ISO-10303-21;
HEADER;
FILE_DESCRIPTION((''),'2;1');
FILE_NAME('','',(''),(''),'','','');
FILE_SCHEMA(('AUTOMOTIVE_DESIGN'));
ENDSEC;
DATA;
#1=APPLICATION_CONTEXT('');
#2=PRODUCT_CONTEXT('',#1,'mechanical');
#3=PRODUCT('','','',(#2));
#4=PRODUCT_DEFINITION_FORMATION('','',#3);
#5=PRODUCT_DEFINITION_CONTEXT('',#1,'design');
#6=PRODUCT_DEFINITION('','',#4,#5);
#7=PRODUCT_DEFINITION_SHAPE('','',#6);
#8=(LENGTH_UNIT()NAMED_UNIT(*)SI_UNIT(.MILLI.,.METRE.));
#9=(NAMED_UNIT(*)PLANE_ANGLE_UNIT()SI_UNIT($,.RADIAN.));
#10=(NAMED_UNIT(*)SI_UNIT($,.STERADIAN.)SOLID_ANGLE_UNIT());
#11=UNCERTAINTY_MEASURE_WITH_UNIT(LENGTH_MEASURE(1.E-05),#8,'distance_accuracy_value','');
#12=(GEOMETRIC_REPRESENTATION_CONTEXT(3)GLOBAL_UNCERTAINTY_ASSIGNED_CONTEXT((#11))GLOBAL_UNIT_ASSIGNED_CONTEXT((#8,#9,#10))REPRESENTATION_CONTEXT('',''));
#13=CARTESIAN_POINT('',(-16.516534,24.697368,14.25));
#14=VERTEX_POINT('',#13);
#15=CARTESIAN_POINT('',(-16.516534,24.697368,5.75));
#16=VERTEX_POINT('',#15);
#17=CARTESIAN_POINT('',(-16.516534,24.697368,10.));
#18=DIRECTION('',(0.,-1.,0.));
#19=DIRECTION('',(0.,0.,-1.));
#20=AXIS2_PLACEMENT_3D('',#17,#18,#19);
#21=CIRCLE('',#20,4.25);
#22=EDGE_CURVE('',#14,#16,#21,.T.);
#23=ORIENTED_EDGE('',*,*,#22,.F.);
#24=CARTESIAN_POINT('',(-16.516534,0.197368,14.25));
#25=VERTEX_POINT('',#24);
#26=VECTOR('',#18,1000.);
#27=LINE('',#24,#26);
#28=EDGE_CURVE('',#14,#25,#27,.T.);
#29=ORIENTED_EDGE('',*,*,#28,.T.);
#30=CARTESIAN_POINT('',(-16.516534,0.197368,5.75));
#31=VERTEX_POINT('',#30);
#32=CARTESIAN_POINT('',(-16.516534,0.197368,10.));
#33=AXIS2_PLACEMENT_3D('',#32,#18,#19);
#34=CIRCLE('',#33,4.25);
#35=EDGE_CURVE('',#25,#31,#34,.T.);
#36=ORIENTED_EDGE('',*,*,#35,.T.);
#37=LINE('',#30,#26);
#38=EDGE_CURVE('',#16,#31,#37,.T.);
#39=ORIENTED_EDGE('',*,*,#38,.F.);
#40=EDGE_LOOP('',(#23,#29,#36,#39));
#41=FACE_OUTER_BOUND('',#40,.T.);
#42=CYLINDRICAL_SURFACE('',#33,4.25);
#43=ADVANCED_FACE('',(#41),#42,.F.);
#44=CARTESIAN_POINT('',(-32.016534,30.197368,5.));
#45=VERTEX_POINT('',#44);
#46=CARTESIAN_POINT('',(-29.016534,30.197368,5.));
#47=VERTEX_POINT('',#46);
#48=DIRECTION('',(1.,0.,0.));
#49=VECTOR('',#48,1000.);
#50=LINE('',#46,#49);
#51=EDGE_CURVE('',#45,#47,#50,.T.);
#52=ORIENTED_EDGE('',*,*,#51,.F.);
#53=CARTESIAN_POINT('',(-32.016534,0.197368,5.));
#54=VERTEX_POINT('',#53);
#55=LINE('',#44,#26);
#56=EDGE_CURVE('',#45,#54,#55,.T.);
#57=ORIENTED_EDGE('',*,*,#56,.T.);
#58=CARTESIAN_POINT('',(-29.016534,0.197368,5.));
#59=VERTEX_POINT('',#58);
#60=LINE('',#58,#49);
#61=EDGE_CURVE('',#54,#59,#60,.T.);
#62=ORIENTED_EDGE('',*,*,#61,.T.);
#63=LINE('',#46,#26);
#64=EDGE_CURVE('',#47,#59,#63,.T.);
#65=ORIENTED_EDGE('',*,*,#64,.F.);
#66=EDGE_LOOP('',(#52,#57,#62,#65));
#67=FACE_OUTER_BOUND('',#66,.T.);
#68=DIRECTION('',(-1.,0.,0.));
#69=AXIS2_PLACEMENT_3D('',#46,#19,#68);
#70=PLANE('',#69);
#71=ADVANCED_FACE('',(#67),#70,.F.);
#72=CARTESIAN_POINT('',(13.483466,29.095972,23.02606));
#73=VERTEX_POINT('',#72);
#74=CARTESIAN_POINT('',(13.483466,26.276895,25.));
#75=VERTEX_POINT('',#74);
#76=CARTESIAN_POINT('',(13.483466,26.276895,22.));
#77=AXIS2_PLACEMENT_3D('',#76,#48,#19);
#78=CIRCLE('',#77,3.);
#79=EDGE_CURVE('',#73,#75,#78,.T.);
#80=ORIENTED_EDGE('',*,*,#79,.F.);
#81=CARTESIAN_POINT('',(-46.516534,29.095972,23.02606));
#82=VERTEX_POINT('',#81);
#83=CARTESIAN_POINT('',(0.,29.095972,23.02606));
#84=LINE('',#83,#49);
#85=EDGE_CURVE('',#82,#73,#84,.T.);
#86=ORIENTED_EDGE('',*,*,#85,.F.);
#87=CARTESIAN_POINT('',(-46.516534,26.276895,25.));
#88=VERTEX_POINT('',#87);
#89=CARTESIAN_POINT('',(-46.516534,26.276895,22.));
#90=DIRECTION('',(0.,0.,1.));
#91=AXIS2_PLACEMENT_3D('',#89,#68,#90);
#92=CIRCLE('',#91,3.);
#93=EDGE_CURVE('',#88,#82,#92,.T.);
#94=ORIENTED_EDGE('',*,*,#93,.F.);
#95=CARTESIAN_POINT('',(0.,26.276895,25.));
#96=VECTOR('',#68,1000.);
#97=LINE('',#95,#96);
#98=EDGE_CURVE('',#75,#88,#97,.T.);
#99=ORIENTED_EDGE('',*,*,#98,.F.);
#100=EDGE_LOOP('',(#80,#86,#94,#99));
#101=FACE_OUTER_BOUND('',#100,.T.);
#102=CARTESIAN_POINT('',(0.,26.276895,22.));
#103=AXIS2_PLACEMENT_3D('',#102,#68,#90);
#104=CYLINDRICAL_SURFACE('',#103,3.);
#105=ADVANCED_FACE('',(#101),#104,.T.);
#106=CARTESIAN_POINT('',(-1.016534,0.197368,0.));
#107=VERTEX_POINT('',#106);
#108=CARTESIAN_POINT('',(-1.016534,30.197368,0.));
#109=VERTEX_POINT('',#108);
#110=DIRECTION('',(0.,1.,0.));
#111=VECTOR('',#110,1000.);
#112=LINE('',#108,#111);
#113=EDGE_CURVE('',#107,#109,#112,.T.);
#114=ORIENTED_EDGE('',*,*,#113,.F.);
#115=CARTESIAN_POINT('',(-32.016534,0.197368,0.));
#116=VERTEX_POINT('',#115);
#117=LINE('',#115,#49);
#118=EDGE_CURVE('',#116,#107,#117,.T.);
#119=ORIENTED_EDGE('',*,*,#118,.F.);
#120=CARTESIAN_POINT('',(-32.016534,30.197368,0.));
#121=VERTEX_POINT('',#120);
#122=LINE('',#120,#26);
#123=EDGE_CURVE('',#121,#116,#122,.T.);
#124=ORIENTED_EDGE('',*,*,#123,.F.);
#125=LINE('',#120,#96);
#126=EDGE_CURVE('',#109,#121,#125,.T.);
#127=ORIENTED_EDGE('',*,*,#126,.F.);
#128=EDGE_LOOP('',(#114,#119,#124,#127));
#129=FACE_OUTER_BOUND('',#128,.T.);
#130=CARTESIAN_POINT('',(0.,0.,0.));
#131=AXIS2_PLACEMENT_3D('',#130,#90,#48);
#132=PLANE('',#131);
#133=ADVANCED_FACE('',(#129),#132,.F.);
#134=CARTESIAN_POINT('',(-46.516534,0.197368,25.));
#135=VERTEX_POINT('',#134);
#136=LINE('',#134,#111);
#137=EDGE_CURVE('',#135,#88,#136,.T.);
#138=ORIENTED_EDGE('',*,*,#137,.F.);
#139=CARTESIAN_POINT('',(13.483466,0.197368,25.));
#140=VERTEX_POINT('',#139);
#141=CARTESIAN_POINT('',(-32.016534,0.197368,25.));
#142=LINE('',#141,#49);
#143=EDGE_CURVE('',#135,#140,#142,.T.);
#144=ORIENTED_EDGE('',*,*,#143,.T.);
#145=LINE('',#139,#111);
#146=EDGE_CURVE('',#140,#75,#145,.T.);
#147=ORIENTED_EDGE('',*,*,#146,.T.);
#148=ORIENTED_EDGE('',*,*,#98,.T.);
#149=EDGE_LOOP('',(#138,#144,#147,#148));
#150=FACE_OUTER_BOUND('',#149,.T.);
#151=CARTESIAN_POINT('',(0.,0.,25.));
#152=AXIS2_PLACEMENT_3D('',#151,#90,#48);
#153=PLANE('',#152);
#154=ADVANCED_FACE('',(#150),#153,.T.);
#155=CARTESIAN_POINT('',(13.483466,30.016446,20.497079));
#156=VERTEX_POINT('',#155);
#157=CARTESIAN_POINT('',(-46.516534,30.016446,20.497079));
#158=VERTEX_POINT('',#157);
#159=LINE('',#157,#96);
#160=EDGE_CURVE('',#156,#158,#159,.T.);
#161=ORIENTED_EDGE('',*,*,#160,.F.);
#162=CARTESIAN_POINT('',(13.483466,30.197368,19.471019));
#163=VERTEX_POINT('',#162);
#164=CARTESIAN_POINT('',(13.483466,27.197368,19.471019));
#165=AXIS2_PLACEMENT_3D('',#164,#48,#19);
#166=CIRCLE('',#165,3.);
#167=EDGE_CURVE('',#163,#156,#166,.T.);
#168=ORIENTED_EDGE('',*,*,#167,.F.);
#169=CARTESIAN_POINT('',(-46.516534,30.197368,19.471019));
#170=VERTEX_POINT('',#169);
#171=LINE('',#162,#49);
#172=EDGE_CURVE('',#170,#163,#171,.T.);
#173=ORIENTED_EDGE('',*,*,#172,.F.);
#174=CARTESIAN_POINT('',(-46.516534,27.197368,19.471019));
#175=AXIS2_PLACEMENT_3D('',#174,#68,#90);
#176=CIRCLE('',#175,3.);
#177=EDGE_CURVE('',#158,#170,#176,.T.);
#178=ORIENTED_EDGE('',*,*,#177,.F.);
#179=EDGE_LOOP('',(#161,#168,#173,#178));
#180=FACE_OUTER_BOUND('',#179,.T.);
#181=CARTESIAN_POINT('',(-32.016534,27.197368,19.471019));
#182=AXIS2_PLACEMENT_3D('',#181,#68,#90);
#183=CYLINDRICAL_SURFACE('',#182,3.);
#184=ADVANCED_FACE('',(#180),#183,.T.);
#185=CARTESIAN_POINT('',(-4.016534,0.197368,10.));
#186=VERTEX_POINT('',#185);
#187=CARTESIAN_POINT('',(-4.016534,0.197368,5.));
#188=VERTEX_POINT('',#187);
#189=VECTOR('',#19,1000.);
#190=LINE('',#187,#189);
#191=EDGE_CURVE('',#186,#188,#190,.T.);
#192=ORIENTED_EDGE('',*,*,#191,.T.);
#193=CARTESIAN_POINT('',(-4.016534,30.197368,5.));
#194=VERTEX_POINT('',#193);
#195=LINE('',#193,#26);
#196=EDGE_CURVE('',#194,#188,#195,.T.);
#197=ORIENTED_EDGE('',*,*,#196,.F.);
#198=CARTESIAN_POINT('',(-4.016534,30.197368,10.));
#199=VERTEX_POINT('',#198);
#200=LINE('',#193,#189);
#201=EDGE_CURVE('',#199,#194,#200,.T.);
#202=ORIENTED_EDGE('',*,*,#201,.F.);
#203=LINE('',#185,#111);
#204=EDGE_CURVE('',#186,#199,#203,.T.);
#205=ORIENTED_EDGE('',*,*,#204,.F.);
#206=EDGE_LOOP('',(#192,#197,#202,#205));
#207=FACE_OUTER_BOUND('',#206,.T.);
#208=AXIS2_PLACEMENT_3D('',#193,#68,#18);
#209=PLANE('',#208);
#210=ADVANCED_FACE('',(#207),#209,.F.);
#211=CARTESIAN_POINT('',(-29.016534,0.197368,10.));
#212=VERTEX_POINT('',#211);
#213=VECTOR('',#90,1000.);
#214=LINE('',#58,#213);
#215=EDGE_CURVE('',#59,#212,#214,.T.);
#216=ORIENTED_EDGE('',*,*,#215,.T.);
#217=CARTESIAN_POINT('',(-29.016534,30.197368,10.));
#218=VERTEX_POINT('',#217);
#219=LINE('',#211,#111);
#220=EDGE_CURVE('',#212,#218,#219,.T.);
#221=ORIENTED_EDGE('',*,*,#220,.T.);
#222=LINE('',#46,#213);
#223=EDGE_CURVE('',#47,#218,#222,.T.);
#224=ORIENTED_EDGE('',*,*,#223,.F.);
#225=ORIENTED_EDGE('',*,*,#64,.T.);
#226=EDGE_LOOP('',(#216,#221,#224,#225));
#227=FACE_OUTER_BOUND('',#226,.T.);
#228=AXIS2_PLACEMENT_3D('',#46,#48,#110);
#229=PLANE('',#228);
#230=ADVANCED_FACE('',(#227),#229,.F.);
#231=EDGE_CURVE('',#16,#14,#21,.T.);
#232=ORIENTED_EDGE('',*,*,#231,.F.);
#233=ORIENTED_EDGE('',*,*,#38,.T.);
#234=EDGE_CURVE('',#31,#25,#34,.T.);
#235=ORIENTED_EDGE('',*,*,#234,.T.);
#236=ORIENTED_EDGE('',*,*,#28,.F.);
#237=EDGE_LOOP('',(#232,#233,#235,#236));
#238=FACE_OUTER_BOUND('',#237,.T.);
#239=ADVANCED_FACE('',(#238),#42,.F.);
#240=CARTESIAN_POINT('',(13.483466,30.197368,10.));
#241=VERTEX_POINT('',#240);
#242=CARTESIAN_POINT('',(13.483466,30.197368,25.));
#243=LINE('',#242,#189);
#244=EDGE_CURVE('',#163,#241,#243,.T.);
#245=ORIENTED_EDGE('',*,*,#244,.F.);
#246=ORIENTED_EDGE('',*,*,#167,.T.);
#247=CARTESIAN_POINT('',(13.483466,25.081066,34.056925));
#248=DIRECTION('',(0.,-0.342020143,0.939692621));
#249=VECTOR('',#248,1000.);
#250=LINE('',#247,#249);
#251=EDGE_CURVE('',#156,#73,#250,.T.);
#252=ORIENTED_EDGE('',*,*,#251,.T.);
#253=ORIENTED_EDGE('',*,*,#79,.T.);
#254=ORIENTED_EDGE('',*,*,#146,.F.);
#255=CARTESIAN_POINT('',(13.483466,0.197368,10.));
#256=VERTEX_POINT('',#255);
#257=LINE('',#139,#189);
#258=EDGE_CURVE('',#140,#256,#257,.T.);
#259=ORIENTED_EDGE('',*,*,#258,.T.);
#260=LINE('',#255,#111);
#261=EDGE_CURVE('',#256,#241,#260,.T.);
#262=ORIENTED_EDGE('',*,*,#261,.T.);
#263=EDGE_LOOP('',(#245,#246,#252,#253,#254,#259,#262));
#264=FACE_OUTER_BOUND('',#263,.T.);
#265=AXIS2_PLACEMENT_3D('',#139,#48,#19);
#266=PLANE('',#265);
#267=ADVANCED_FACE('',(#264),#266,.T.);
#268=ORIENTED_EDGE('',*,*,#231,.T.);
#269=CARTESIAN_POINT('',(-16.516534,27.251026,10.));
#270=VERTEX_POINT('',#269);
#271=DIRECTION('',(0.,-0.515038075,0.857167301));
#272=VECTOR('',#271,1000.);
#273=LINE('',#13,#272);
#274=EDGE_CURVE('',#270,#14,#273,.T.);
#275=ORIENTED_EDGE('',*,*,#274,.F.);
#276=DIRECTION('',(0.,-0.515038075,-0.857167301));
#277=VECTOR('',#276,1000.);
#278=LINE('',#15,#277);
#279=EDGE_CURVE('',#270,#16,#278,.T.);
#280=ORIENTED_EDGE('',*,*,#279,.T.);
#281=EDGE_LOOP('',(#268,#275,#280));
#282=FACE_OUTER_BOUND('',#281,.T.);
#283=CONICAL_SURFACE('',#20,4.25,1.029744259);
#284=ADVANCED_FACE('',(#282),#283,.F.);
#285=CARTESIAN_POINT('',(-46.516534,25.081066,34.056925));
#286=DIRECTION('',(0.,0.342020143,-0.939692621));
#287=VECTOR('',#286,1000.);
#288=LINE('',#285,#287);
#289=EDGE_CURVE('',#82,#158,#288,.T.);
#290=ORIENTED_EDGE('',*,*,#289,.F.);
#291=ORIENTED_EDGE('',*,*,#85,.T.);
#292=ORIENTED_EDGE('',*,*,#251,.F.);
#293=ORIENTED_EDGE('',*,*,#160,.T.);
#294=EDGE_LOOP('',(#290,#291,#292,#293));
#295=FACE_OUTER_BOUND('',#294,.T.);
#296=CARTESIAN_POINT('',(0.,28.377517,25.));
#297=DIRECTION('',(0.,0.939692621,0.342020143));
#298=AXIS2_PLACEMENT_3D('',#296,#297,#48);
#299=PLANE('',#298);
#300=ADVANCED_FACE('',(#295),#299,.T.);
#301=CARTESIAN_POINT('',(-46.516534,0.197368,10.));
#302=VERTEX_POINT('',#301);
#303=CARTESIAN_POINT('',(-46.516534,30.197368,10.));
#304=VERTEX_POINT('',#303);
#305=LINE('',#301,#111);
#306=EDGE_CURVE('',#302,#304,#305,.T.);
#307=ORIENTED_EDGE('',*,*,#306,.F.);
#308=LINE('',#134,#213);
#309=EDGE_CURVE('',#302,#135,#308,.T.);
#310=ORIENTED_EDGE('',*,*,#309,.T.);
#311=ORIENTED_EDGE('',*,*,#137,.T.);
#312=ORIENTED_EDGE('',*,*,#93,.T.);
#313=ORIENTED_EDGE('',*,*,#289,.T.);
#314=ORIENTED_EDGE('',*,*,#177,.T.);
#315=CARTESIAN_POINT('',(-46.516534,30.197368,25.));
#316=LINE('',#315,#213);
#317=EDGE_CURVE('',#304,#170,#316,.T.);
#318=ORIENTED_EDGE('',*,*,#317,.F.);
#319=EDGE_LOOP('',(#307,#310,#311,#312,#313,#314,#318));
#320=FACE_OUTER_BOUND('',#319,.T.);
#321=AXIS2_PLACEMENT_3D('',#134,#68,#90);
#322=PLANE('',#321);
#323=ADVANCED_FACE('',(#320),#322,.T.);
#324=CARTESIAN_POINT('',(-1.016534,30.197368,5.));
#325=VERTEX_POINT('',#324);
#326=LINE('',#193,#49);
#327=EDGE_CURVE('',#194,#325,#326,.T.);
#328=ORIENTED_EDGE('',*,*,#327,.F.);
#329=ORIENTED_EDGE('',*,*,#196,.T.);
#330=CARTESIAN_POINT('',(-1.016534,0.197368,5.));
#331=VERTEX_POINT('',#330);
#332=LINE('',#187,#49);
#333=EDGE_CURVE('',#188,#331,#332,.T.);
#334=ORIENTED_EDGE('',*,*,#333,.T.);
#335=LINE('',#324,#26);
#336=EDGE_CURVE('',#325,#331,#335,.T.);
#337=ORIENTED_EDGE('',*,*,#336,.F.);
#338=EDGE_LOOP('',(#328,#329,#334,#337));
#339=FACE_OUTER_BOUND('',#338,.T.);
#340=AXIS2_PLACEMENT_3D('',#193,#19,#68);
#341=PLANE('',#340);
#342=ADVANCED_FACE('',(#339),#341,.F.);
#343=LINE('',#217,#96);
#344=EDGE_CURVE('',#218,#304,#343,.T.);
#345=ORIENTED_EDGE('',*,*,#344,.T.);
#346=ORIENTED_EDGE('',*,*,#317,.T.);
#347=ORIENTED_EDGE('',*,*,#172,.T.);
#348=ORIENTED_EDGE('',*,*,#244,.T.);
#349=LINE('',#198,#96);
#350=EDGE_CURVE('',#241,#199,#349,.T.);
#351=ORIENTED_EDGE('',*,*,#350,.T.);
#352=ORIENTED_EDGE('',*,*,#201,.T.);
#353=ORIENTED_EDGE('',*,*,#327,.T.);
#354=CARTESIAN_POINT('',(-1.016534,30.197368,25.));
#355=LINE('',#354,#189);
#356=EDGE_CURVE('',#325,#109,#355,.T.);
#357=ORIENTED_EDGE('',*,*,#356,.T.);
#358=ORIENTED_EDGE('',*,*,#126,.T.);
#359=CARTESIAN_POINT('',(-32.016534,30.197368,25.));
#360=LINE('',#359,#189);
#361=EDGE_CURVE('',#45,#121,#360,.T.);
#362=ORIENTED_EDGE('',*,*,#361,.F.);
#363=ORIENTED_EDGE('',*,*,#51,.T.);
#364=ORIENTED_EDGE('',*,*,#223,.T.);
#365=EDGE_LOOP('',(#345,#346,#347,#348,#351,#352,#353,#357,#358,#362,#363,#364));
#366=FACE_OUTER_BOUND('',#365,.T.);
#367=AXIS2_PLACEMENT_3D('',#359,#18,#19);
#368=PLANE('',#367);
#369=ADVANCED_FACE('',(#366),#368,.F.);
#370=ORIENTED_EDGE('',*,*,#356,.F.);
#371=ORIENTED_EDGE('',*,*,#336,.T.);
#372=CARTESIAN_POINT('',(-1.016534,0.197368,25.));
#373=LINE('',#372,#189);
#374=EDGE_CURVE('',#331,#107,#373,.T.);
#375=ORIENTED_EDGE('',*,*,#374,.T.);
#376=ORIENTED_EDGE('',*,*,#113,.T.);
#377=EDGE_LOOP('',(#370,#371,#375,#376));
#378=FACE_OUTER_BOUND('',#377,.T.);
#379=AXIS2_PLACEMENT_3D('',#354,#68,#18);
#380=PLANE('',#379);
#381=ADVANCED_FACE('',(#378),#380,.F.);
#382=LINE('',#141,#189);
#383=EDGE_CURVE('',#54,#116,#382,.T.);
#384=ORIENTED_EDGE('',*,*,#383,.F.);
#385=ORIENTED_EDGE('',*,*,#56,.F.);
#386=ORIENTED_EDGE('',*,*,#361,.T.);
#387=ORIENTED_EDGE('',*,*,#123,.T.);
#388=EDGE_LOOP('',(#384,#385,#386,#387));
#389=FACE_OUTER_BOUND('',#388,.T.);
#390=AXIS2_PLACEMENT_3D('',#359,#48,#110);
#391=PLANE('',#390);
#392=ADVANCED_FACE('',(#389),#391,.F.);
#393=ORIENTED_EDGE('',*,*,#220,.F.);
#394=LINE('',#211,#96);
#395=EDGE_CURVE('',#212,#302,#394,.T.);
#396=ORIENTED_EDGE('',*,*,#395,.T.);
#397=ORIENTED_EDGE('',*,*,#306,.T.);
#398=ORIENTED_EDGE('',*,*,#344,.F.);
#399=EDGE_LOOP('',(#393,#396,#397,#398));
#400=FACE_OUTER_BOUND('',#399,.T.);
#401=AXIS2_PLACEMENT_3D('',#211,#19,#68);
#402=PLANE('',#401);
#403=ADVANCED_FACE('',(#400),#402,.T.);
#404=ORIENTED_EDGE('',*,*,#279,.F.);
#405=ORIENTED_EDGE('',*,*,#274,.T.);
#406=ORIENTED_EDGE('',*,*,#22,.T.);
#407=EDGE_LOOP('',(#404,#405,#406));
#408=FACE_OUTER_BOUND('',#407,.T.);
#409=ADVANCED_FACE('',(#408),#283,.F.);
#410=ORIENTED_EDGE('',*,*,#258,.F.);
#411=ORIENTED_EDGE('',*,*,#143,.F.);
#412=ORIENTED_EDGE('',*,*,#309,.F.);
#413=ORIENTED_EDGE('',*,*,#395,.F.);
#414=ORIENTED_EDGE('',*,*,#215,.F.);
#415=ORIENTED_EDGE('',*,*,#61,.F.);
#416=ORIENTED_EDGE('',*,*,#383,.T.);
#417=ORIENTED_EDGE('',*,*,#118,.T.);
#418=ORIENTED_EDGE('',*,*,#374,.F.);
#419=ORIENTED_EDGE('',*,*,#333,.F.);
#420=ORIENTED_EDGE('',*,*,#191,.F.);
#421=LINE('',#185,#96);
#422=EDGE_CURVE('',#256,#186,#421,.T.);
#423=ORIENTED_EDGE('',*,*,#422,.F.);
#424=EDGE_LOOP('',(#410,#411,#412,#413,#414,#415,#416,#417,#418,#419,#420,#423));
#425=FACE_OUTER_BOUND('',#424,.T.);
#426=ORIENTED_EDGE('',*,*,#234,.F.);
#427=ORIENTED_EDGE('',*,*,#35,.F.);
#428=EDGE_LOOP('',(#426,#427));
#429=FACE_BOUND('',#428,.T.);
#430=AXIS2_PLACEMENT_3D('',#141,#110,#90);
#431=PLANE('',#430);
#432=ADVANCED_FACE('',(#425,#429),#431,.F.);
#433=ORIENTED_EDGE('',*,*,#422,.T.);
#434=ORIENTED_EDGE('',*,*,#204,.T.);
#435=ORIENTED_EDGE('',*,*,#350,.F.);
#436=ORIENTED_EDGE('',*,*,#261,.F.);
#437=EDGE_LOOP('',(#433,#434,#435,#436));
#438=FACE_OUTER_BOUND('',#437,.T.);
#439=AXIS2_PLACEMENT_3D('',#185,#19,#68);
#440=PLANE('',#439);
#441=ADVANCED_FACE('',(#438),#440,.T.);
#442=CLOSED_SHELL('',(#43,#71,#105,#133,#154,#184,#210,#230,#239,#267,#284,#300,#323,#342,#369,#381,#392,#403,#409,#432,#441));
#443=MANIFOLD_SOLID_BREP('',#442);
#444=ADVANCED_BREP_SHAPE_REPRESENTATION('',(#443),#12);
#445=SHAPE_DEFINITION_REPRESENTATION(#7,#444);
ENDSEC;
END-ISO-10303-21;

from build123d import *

# Parameters (mm, degrees)
SKETCH1_W              = 31
SKETCH1_H              = 30
BOSS_EXTRUDE1_DEPTH    = 25
SKETCH2_W              = 3
SKETCH2_H              = 20
CUT_EXTRUDE1_DEPTH     = 51.498103381
SKETCH3_W              = 17.5
SKETCH3_H              = 15
BOSS_EXTRUDE2_DEPTH    = 30
CHAMFER1_SIZE          = 5
CHAMFER1_SIZE2         = 1.819851171
FILLET1_R              = 3
M10_TAPPED_HOLE1_D     = 8.5
M10_TAPPED_HOLE1_DEPTH = 24.5
M10_TAPPED_HOLE1_TIP   = 2.553657631


with BuildPart() as part:
    # Sketch1 → Boss-Extrude1 (new body)
    with BuildSketch(Plane.XY):
        with Locations((-16.516533934, 15.197368421)):
            Rectangle(SKETCH1_W, SKETCH1_H)
    extrude(amount=BOSS_EXTRUDE1_DEPTH)

    # Sketch2 → Cut-Extrude1 (cut, through all)
    with BuildSketch(Plane.XZ.offset(-0.197368421)):
        with Locations((-30.516533934, 15)):
            Rectangle(SKETCH2_W, SKETCH2_H)
        with Locations((-2.516533934, 15)):
            Rectangle(SKETCH2_W, SKETCH2_H)
    extrude(amount=-CUT_EXTRUDE1_DEPTH, mode=Mode.SUBTRACT)

    # Sketch3 → Boss-Extrude2 (add, through all)
    with BuildSketch(Plane(origin=(0, 30.197368421, 0), x_dir=(1, 0, 0), z_dir=(0, 1, 0))):
        with Locations((4.733466066, -17.5)):
            Rectangle(SKETCH3_W, SKETCH3_H)
        with Locations((-37.766533934, -17.5)):
            Rectangle(SKETCH3_W, SKETCH3_H)
    extrude(amount=-BOSS_EXTRUDE2_DEPTH)

    # Chamfer1
    chamfer1_edges = [part.edges().sort_by_distance(p)[0] for p in [
        (-16.516533934, 30.197368421, 25),
    ]]
    chamfer1_side = [part.faces().sort_by_distance(p)[0] for p in [
        (-16.516533934, 30.197368421, 14.470338983),
    ]]
    chamfer(chamfer1_edges, length=CHAMFER1_SIZE, length2=CHAMFER1_SIZE2, reference=chamfer1_side[0])

    # Fillet1
    fillet1_edges = [part.edges().sort_by_distance(p)[0] for p in [
        (-16.516533934, 28.37751725, 25),
        (-16.516533934, 30.197368421, 20),
    ]]
    fillet(fillet1_edges, radius=FILLET1_R)

    # M10 Tapped Hole1
    with Locations(Plane(origin=(0, 0.197368421, 0), x_dir=(-1, 0, 0), z_dir=(0, -1, 0))):
        with Locations((16.516533934, -10)):
            Hole(M10_TAPPED_HOLE1_D / 2, depth=M10_TAPPED_HOLE1_DEPTH)
            with Locations((0, 0, -(M10_TAPPED_HOLE1_DEPTH + M10_TAPPED_HOLE1_TIP / 2))):  # 118° drill point
                Cone(0, M10_TAPPED_HOLE1_D / 2, M10_TAPPED_HOLE1_TIP, mode=Mode.SUBTRACT)


solid = part.part
